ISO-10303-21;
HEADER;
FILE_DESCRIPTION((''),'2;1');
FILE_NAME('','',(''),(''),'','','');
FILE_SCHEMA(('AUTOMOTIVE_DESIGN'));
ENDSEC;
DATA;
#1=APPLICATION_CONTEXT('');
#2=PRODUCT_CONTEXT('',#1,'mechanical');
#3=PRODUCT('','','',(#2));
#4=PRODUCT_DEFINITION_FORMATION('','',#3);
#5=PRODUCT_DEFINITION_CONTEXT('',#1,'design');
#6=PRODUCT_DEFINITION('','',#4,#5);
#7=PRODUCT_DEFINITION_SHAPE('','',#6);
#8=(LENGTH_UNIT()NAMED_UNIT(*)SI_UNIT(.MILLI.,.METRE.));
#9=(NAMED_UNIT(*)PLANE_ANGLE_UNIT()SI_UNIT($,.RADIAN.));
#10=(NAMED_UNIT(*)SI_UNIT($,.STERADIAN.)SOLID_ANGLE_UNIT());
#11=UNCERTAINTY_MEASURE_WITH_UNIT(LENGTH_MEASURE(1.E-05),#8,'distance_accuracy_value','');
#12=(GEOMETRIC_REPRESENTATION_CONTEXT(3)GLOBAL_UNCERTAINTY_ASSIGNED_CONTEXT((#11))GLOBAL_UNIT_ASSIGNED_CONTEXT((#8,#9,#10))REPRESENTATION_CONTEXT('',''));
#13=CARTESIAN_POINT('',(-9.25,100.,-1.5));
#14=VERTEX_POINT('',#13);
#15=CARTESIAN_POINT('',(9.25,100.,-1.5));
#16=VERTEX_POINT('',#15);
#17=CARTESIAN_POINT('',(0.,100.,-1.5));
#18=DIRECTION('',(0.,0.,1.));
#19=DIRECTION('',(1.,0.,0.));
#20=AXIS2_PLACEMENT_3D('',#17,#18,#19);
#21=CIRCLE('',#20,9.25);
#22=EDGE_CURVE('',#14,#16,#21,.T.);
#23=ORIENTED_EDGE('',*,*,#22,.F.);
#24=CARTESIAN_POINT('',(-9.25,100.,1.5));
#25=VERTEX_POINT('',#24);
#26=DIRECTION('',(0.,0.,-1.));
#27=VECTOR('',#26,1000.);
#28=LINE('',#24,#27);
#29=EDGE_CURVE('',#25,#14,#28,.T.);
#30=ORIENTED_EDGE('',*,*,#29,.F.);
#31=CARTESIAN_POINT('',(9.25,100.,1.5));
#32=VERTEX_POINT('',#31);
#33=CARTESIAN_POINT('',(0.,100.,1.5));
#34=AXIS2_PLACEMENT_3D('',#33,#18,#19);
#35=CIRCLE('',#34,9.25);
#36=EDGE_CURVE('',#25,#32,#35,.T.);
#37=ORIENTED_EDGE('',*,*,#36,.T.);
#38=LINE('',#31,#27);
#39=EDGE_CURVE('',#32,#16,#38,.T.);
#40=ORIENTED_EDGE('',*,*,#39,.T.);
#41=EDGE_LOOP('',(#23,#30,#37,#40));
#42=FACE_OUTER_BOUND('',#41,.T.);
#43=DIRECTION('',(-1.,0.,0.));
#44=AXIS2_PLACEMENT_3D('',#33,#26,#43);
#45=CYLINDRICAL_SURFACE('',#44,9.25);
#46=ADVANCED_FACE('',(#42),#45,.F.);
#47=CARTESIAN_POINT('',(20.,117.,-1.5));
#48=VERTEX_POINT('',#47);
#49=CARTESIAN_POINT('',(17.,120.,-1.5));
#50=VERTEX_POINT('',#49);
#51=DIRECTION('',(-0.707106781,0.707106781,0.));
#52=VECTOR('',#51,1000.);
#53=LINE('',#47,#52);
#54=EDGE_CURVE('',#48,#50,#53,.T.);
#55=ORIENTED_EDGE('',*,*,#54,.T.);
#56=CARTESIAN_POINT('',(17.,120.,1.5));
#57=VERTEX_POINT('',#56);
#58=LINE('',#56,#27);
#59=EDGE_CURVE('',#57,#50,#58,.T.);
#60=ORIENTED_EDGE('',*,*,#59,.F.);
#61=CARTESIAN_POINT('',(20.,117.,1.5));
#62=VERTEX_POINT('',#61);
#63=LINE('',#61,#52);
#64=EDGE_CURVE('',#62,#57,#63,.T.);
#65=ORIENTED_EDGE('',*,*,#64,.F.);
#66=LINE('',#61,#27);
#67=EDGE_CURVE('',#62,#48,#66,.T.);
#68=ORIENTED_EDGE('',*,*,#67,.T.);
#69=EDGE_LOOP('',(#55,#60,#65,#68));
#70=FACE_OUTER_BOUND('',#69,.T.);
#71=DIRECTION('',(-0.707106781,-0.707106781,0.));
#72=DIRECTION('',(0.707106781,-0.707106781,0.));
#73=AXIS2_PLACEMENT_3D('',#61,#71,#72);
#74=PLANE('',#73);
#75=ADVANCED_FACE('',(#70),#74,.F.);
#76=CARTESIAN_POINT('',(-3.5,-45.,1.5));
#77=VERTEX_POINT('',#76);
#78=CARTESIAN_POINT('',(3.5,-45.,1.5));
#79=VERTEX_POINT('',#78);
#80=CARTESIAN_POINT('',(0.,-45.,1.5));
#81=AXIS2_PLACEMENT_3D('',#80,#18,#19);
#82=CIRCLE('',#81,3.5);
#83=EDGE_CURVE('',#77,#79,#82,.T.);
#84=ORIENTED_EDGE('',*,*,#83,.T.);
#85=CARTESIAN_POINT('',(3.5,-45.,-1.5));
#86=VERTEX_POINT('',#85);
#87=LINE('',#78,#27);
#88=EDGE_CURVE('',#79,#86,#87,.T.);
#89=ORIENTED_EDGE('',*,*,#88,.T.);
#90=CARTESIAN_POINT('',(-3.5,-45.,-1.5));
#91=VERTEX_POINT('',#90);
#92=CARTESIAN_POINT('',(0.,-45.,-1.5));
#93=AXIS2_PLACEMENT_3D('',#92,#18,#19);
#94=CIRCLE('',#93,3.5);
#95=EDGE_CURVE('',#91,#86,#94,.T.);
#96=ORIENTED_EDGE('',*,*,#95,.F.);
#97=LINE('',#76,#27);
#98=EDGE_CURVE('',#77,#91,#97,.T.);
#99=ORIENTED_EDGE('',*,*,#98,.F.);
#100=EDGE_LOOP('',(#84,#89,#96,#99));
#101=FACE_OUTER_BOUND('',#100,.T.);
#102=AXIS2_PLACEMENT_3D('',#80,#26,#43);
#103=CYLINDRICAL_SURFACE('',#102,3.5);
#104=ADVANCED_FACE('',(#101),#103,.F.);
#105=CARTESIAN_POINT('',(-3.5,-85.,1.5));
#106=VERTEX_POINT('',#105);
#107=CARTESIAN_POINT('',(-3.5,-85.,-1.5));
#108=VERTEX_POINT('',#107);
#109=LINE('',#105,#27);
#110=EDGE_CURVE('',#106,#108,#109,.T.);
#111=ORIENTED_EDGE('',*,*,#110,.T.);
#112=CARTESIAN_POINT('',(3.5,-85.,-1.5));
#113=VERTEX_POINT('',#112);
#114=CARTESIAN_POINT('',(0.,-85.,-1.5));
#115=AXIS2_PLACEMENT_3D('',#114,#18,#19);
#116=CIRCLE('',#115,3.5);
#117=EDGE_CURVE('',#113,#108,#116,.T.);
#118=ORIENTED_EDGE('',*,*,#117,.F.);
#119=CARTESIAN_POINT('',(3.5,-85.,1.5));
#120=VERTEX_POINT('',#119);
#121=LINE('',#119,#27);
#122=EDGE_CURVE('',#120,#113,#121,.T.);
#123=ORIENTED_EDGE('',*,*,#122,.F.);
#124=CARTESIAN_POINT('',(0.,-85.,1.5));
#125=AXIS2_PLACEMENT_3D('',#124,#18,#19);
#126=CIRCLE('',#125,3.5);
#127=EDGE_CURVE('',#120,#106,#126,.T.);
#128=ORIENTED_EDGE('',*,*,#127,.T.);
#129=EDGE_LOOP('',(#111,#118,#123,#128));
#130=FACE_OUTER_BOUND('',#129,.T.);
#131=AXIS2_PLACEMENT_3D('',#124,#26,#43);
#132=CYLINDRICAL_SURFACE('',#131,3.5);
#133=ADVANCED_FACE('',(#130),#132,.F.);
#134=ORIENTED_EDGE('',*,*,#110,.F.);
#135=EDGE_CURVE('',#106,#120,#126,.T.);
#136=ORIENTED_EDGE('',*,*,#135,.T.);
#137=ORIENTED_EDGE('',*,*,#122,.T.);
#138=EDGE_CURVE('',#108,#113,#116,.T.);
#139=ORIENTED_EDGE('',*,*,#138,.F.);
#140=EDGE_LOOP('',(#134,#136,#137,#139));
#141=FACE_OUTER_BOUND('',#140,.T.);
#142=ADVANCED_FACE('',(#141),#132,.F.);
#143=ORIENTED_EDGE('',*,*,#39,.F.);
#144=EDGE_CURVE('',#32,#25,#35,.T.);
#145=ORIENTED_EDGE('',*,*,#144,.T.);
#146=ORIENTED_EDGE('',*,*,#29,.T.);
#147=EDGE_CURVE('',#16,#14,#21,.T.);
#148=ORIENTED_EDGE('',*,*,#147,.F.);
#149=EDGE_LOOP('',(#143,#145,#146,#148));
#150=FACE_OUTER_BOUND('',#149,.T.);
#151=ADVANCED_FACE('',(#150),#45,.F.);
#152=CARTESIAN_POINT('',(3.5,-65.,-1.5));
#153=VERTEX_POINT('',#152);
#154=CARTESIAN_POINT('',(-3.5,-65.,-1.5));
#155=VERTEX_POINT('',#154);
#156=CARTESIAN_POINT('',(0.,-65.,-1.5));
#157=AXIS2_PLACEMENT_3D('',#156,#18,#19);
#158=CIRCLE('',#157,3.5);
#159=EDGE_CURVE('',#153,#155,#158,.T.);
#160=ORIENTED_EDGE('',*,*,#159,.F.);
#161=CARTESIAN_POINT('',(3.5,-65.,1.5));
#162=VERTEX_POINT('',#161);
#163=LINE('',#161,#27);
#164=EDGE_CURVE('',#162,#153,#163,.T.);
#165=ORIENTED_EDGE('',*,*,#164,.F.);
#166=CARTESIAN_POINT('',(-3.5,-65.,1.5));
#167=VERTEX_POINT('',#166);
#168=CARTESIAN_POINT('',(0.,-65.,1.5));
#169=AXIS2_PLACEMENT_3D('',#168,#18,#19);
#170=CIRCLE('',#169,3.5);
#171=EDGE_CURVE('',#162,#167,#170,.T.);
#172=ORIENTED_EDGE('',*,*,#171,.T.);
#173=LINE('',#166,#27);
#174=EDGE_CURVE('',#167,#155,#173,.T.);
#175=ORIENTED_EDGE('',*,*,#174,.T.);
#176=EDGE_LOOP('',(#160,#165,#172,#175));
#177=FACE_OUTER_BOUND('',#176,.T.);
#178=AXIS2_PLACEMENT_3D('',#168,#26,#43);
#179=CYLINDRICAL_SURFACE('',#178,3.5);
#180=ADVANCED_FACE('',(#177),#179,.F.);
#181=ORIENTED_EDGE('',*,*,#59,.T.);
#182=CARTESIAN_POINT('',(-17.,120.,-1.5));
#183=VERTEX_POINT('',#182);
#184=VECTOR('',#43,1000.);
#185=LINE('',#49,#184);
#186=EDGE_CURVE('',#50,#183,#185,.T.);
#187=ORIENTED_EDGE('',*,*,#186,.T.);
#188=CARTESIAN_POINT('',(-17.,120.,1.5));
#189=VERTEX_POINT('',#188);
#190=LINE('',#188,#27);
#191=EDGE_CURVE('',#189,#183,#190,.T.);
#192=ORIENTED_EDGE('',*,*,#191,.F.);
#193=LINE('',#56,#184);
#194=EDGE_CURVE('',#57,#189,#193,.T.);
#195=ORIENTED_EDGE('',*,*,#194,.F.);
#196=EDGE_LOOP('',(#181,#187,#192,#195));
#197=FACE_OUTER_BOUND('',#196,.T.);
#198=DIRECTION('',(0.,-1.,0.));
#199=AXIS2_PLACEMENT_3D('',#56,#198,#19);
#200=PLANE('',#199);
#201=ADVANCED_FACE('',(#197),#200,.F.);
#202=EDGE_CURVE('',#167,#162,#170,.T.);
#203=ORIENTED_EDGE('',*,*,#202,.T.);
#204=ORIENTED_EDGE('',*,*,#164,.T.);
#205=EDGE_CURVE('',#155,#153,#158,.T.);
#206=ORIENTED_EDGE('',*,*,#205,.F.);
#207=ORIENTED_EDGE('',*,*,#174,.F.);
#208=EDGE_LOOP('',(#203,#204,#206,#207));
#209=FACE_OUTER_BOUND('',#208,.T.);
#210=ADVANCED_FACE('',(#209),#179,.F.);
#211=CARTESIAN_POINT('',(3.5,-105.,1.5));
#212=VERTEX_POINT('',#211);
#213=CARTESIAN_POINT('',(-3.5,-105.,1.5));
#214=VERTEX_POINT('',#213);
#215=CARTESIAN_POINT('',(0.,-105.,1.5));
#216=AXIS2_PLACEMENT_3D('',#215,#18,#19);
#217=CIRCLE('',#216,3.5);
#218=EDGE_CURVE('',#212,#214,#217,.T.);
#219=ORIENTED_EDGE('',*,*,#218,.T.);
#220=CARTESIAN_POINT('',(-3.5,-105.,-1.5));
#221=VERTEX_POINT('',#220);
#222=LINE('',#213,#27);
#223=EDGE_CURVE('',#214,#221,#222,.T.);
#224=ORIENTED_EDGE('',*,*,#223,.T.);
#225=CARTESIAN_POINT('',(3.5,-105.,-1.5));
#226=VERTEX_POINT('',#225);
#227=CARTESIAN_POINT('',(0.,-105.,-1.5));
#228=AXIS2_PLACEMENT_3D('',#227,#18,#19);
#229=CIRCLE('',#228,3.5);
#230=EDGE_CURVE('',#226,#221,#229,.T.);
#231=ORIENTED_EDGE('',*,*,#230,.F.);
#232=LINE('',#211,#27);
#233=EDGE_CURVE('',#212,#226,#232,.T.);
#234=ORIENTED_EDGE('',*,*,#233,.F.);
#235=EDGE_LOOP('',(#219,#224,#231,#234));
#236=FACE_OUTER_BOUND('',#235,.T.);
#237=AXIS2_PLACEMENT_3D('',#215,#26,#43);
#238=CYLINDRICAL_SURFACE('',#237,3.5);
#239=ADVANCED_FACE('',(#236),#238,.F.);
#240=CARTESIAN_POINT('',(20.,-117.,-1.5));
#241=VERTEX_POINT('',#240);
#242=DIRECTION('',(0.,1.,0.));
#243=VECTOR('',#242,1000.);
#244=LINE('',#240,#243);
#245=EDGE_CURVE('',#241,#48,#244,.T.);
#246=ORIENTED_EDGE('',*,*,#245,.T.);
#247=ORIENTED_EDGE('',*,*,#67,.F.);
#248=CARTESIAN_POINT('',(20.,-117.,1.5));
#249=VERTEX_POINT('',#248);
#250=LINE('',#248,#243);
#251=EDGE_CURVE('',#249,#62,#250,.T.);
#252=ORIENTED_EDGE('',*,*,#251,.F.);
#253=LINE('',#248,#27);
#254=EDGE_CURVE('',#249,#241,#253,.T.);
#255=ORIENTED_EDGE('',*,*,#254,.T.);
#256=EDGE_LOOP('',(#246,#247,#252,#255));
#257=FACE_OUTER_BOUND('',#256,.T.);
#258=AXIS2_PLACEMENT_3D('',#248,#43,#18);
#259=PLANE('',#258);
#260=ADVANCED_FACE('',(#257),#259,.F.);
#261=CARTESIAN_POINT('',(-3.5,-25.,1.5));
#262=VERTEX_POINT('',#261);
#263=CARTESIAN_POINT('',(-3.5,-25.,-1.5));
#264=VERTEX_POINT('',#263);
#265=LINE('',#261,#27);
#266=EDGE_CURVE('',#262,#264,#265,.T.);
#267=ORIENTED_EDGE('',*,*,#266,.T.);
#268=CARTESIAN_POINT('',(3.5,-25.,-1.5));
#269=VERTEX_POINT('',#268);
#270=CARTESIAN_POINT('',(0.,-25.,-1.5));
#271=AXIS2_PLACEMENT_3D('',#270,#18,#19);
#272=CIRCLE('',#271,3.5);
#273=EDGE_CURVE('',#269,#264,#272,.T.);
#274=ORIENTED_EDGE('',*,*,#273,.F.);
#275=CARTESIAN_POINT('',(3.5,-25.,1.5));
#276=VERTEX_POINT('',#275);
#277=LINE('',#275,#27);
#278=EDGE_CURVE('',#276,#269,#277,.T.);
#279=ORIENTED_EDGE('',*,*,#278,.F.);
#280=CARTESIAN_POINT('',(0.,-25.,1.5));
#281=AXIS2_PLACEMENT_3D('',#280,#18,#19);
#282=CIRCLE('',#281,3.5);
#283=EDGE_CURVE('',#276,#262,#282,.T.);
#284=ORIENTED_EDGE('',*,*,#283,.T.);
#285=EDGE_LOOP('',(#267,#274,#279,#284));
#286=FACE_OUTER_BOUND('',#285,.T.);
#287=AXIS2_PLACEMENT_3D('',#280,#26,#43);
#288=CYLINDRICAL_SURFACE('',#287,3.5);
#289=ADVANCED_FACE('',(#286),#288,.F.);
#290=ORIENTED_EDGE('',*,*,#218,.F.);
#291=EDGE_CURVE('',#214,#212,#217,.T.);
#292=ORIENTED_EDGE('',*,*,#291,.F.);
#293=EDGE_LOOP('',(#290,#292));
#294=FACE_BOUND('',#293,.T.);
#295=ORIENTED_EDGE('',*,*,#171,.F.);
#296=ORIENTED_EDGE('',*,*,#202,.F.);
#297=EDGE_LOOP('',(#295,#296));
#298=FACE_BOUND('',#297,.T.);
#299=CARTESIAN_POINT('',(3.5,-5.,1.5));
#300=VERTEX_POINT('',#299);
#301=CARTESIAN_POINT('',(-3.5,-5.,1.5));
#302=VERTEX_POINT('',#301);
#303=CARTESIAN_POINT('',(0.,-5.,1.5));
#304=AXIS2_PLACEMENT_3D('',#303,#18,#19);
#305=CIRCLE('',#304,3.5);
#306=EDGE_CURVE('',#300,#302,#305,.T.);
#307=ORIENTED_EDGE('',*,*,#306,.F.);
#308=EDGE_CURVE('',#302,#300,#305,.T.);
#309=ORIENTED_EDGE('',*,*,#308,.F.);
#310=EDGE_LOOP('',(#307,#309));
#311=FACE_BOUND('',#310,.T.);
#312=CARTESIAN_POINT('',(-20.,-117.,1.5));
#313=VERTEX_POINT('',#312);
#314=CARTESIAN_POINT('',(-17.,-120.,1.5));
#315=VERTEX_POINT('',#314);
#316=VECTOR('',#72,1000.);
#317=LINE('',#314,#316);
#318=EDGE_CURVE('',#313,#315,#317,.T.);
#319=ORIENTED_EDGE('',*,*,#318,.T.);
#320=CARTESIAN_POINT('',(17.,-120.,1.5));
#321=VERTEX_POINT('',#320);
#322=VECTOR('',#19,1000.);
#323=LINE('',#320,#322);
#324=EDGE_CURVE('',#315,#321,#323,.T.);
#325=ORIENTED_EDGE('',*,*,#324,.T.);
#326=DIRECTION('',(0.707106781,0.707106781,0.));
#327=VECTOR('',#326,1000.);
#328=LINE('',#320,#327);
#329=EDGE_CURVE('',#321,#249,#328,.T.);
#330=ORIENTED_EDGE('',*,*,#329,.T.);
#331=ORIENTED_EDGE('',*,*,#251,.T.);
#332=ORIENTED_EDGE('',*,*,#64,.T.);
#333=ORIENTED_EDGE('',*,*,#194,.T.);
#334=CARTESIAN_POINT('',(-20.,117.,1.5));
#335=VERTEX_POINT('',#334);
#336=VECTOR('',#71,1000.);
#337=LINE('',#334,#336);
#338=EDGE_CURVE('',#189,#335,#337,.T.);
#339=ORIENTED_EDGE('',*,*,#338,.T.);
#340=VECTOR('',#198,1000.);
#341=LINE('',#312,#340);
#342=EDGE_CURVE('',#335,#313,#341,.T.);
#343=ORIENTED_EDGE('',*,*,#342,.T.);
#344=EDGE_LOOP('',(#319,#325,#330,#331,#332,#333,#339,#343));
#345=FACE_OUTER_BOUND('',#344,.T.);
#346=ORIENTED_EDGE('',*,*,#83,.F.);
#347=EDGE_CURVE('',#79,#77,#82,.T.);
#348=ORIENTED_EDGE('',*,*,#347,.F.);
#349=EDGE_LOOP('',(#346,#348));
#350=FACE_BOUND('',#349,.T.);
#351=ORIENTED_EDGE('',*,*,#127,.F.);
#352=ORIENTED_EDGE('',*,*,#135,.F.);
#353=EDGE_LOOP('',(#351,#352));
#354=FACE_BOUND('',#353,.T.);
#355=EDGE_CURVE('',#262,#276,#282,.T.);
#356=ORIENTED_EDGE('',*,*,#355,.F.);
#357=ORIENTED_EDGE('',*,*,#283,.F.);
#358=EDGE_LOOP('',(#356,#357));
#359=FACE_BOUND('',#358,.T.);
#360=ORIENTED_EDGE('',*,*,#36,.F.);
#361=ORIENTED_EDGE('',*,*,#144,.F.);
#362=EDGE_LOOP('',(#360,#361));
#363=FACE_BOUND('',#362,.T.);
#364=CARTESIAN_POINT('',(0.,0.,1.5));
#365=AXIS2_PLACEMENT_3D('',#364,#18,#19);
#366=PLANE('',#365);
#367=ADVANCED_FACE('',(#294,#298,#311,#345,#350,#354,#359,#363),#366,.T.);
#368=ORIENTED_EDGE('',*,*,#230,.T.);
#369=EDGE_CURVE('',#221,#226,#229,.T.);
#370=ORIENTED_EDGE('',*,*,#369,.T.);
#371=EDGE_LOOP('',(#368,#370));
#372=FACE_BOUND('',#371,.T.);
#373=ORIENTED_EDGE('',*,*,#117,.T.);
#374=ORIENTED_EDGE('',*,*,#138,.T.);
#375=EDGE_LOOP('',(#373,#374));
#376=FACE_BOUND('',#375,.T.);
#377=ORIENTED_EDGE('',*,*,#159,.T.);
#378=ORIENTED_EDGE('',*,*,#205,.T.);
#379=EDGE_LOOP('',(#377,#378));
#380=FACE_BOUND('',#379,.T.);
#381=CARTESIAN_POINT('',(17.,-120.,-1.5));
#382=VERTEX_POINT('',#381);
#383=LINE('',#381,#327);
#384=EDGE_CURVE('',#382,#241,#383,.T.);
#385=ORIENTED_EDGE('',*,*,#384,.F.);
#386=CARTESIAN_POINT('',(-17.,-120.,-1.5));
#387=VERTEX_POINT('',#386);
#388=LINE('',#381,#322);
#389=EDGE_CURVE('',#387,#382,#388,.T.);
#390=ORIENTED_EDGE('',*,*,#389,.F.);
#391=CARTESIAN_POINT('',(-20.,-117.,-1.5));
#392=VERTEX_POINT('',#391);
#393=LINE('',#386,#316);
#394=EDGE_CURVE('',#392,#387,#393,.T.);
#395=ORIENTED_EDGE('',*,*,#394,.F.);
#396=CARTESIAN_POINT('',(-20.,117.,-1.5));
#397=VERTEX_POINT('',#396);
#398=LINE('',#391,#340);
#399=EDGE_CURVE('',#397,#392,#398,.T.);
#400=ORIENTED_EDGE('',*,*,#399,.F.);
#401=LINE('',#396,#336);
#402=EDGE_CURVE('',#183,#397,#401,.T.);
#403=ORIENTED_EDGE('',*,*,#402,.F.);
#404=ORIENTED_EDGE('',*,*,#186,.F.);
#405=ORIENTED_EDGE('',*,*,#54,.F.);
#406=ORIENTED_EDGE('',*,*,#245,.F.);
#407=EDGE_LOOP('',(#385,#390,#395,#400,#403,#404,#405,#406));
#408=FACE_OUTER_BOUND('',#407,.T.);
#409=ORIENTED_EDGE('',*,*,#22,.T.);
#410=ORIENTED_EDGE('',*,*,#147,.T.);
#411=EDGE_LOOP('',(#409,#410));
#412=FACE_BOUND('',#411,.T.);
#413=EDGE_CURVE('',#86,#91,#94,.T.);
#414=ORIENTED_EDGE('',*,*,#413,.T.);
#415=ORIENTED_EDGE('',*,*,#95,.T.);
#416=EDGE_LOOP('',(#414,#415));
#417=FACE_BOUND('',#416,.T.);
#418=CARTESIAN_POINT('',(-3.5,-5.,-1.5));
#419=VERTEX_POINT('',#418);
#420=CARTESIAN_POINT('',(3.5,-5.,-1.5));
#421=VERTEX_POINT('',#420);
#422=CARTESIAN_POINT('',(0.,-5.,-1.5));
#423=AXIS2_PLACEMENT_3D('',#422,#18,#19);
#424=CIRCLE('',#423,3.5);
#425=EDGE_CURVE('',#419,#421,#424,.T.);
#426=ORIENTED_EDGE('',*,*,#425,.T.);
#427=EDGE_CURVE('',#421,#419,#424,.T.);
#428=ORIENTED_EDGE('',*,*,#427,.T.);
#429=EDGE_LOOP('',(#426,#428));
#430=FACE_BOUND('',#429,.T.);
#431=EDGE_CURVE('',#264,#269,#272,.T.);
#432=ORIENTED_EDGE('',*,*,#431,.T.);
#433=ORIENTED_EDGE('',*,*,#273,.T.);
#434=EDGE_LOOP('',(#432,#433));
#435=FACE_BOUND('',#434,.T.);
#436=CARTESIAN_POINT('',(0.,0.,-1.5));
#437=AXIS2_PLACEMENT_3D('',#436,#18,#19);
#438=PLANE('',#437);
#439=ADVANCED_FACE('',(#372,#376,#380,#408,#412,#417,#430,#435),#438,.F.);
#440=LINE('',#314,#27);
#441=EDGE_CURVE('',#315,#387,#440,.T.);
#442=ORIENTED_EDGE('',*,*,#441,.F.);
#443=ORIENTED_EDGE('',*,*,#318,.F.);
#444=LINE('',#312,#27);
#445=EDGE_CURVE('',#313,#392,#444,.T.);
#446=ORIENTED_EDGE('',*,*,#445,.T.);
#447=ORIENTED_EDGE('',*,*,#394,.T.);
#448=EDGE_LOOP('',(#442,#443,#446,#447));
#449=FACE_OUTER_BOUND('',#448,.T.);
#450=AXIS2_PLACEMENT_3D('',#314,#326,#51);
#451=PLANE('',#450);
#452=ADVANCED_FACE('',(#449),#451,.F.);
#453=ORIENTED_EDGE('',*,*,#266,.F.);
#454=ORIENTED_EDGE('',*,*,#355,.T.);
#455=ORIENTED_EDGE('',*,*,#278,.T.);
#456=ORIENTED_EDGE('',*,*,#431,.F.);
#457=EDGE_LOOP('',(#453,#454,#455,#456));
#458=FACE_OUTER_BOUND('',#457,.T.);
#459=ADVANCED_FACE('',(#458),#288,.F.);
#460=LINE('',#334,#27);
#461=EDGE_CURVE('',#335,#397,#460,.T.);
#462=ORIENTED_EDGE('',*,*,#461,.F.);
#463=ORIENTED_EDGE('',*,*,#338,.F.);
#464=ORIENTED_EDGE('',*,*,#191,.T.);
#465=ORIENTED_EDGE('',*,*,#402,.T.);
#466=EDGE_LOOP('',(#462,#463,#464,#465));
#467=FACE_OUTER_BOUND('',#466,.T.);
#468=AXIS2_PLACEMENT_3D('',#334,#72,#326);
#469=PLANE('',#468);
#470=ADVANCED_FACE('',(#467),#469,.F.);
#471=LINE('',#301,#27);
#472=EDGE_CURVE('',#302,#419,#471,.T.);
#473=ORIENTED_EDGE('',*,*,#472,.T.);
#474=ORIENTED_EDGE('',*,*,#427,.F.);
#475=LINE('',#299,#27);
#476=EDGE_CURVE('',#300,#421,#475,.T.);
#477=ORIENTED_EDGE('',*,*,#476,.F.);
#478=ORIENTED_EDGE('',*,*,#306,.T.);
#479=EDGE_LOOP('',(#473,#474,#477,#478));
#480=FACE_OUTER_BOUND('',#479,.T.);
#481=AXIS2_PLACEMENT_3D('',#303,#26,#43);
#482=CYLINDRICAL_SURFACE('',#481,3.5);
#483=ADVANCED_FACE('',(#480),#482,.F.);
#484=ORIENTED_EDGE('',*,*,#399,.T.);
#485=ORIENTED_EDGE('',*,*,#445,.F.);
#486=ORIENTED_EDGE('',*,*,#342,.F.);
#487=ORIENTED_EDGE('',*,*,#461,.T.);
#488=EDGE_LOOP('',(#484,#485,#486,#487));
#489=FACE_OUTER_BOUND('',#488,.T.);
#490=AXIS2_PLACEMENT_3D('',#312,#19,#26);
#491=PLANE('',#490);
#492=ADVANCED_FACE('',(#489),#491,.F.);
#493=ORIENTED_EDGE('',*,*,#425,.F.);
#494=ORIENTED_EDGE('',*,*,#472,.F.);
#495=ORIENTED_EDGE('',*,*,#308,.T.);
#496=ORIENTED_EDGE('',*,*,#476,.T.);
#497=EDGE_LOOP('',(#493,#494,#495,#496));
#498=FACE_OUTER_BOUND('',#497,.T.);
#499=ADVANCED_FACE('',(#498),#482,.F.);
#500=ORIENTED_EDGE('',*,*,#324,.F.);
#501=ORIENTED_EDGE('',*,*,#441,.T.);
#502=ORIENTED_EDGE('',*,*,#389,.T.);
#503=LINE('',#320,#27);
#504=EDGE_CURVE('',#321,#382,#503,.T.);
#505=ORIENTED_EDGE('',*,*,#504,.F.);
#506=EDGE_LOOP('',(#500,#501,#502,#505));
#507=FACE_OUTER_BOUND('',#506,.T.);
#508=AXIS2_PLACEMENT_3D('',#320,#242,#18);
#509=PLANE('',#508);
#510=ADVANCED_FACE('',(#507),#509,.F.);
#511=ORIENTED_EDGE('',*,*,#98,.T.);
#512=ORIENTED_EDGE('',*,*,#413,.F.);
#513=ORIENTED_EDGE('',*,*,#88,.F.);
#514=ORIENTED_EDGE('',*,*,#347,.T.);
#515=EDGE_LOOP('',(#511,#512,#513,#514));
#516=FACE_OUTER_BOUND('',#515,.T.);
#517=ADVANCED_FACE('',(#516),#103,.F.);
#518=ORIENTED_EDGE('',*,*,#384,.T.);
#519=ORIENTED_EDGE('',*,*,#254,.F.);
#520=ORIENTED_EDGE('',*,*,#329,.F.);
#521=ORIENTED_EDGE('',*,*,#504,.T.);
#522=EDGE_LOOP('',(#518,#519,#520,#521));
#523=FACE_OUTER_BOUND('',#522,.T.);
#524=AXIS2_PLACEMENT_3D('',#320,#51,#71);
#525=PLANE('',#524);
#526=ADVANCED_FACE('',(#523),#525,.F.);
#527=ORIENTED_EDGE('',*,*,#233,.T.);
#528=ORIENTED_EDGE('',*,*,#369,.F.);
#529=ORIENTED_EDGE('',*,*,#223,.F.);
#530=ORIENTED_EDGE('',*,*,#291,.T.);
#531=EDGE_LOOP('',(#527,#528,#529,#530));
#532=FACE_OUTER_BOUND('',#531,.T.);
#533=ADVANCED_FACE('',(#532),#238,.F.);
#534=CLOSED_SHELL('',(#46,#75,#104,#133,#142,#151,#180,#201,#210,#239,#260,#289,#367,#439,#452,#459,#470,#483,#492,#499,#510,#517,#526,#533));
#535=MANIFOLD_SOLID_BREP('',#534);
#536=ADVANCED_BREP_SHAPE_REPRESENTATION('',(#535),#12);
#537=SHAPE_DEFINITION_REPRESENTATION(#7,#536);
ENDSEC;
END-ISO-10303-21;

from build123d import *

# Parameters (mm, degrees)
SKETCH1_R           = 9.25
SKETCH1_R_2         = 3.5
BOSS_EXTRUDE1_DEPTH = 1.5


with BuildPart() as part:
    # Sketch1 → Boss-Extrude1 (new, symmetric)
    with BuildSketch(Plane.XY):
        Polygon((-20, 117), (-17, 120), (17, 120), (20, 117), (20, -117), (17, -120), (-17, -120), (-20, -117), align=None)
        with Locations((0, 100)):
            Circle(SKETCH1_R, mode=Mode.SUBTRACT)
        with Locations((0, -105)):
            Circle(SKETCH1_R_2, mode=Mode.SUBTRACT)
        with Locations((0, -85)):
            Circle(SKETCH1_R_2, mode=Mode.SUBTRACT)
        with Locations((0, -65)):
            Circle(SKETCH1_R_2, mode=Mode.SUBTRACT)
        with Locations((0, -45)):
            Circle(SKETCH1_R_2, mode=Mode.SUBTRACT)
        with Locations((0, -25)):
            Circle(SKETCH1_R_2, mode=Mode.SUBTRACT)
        with Locations((0, -5)):
            Circle(SKETCH1_R_2, mode=Mode.SUBTRACT)
    extrude(amount=BOSS_EXTRUDE1_DEPTH, both=True)


solid = part.part
